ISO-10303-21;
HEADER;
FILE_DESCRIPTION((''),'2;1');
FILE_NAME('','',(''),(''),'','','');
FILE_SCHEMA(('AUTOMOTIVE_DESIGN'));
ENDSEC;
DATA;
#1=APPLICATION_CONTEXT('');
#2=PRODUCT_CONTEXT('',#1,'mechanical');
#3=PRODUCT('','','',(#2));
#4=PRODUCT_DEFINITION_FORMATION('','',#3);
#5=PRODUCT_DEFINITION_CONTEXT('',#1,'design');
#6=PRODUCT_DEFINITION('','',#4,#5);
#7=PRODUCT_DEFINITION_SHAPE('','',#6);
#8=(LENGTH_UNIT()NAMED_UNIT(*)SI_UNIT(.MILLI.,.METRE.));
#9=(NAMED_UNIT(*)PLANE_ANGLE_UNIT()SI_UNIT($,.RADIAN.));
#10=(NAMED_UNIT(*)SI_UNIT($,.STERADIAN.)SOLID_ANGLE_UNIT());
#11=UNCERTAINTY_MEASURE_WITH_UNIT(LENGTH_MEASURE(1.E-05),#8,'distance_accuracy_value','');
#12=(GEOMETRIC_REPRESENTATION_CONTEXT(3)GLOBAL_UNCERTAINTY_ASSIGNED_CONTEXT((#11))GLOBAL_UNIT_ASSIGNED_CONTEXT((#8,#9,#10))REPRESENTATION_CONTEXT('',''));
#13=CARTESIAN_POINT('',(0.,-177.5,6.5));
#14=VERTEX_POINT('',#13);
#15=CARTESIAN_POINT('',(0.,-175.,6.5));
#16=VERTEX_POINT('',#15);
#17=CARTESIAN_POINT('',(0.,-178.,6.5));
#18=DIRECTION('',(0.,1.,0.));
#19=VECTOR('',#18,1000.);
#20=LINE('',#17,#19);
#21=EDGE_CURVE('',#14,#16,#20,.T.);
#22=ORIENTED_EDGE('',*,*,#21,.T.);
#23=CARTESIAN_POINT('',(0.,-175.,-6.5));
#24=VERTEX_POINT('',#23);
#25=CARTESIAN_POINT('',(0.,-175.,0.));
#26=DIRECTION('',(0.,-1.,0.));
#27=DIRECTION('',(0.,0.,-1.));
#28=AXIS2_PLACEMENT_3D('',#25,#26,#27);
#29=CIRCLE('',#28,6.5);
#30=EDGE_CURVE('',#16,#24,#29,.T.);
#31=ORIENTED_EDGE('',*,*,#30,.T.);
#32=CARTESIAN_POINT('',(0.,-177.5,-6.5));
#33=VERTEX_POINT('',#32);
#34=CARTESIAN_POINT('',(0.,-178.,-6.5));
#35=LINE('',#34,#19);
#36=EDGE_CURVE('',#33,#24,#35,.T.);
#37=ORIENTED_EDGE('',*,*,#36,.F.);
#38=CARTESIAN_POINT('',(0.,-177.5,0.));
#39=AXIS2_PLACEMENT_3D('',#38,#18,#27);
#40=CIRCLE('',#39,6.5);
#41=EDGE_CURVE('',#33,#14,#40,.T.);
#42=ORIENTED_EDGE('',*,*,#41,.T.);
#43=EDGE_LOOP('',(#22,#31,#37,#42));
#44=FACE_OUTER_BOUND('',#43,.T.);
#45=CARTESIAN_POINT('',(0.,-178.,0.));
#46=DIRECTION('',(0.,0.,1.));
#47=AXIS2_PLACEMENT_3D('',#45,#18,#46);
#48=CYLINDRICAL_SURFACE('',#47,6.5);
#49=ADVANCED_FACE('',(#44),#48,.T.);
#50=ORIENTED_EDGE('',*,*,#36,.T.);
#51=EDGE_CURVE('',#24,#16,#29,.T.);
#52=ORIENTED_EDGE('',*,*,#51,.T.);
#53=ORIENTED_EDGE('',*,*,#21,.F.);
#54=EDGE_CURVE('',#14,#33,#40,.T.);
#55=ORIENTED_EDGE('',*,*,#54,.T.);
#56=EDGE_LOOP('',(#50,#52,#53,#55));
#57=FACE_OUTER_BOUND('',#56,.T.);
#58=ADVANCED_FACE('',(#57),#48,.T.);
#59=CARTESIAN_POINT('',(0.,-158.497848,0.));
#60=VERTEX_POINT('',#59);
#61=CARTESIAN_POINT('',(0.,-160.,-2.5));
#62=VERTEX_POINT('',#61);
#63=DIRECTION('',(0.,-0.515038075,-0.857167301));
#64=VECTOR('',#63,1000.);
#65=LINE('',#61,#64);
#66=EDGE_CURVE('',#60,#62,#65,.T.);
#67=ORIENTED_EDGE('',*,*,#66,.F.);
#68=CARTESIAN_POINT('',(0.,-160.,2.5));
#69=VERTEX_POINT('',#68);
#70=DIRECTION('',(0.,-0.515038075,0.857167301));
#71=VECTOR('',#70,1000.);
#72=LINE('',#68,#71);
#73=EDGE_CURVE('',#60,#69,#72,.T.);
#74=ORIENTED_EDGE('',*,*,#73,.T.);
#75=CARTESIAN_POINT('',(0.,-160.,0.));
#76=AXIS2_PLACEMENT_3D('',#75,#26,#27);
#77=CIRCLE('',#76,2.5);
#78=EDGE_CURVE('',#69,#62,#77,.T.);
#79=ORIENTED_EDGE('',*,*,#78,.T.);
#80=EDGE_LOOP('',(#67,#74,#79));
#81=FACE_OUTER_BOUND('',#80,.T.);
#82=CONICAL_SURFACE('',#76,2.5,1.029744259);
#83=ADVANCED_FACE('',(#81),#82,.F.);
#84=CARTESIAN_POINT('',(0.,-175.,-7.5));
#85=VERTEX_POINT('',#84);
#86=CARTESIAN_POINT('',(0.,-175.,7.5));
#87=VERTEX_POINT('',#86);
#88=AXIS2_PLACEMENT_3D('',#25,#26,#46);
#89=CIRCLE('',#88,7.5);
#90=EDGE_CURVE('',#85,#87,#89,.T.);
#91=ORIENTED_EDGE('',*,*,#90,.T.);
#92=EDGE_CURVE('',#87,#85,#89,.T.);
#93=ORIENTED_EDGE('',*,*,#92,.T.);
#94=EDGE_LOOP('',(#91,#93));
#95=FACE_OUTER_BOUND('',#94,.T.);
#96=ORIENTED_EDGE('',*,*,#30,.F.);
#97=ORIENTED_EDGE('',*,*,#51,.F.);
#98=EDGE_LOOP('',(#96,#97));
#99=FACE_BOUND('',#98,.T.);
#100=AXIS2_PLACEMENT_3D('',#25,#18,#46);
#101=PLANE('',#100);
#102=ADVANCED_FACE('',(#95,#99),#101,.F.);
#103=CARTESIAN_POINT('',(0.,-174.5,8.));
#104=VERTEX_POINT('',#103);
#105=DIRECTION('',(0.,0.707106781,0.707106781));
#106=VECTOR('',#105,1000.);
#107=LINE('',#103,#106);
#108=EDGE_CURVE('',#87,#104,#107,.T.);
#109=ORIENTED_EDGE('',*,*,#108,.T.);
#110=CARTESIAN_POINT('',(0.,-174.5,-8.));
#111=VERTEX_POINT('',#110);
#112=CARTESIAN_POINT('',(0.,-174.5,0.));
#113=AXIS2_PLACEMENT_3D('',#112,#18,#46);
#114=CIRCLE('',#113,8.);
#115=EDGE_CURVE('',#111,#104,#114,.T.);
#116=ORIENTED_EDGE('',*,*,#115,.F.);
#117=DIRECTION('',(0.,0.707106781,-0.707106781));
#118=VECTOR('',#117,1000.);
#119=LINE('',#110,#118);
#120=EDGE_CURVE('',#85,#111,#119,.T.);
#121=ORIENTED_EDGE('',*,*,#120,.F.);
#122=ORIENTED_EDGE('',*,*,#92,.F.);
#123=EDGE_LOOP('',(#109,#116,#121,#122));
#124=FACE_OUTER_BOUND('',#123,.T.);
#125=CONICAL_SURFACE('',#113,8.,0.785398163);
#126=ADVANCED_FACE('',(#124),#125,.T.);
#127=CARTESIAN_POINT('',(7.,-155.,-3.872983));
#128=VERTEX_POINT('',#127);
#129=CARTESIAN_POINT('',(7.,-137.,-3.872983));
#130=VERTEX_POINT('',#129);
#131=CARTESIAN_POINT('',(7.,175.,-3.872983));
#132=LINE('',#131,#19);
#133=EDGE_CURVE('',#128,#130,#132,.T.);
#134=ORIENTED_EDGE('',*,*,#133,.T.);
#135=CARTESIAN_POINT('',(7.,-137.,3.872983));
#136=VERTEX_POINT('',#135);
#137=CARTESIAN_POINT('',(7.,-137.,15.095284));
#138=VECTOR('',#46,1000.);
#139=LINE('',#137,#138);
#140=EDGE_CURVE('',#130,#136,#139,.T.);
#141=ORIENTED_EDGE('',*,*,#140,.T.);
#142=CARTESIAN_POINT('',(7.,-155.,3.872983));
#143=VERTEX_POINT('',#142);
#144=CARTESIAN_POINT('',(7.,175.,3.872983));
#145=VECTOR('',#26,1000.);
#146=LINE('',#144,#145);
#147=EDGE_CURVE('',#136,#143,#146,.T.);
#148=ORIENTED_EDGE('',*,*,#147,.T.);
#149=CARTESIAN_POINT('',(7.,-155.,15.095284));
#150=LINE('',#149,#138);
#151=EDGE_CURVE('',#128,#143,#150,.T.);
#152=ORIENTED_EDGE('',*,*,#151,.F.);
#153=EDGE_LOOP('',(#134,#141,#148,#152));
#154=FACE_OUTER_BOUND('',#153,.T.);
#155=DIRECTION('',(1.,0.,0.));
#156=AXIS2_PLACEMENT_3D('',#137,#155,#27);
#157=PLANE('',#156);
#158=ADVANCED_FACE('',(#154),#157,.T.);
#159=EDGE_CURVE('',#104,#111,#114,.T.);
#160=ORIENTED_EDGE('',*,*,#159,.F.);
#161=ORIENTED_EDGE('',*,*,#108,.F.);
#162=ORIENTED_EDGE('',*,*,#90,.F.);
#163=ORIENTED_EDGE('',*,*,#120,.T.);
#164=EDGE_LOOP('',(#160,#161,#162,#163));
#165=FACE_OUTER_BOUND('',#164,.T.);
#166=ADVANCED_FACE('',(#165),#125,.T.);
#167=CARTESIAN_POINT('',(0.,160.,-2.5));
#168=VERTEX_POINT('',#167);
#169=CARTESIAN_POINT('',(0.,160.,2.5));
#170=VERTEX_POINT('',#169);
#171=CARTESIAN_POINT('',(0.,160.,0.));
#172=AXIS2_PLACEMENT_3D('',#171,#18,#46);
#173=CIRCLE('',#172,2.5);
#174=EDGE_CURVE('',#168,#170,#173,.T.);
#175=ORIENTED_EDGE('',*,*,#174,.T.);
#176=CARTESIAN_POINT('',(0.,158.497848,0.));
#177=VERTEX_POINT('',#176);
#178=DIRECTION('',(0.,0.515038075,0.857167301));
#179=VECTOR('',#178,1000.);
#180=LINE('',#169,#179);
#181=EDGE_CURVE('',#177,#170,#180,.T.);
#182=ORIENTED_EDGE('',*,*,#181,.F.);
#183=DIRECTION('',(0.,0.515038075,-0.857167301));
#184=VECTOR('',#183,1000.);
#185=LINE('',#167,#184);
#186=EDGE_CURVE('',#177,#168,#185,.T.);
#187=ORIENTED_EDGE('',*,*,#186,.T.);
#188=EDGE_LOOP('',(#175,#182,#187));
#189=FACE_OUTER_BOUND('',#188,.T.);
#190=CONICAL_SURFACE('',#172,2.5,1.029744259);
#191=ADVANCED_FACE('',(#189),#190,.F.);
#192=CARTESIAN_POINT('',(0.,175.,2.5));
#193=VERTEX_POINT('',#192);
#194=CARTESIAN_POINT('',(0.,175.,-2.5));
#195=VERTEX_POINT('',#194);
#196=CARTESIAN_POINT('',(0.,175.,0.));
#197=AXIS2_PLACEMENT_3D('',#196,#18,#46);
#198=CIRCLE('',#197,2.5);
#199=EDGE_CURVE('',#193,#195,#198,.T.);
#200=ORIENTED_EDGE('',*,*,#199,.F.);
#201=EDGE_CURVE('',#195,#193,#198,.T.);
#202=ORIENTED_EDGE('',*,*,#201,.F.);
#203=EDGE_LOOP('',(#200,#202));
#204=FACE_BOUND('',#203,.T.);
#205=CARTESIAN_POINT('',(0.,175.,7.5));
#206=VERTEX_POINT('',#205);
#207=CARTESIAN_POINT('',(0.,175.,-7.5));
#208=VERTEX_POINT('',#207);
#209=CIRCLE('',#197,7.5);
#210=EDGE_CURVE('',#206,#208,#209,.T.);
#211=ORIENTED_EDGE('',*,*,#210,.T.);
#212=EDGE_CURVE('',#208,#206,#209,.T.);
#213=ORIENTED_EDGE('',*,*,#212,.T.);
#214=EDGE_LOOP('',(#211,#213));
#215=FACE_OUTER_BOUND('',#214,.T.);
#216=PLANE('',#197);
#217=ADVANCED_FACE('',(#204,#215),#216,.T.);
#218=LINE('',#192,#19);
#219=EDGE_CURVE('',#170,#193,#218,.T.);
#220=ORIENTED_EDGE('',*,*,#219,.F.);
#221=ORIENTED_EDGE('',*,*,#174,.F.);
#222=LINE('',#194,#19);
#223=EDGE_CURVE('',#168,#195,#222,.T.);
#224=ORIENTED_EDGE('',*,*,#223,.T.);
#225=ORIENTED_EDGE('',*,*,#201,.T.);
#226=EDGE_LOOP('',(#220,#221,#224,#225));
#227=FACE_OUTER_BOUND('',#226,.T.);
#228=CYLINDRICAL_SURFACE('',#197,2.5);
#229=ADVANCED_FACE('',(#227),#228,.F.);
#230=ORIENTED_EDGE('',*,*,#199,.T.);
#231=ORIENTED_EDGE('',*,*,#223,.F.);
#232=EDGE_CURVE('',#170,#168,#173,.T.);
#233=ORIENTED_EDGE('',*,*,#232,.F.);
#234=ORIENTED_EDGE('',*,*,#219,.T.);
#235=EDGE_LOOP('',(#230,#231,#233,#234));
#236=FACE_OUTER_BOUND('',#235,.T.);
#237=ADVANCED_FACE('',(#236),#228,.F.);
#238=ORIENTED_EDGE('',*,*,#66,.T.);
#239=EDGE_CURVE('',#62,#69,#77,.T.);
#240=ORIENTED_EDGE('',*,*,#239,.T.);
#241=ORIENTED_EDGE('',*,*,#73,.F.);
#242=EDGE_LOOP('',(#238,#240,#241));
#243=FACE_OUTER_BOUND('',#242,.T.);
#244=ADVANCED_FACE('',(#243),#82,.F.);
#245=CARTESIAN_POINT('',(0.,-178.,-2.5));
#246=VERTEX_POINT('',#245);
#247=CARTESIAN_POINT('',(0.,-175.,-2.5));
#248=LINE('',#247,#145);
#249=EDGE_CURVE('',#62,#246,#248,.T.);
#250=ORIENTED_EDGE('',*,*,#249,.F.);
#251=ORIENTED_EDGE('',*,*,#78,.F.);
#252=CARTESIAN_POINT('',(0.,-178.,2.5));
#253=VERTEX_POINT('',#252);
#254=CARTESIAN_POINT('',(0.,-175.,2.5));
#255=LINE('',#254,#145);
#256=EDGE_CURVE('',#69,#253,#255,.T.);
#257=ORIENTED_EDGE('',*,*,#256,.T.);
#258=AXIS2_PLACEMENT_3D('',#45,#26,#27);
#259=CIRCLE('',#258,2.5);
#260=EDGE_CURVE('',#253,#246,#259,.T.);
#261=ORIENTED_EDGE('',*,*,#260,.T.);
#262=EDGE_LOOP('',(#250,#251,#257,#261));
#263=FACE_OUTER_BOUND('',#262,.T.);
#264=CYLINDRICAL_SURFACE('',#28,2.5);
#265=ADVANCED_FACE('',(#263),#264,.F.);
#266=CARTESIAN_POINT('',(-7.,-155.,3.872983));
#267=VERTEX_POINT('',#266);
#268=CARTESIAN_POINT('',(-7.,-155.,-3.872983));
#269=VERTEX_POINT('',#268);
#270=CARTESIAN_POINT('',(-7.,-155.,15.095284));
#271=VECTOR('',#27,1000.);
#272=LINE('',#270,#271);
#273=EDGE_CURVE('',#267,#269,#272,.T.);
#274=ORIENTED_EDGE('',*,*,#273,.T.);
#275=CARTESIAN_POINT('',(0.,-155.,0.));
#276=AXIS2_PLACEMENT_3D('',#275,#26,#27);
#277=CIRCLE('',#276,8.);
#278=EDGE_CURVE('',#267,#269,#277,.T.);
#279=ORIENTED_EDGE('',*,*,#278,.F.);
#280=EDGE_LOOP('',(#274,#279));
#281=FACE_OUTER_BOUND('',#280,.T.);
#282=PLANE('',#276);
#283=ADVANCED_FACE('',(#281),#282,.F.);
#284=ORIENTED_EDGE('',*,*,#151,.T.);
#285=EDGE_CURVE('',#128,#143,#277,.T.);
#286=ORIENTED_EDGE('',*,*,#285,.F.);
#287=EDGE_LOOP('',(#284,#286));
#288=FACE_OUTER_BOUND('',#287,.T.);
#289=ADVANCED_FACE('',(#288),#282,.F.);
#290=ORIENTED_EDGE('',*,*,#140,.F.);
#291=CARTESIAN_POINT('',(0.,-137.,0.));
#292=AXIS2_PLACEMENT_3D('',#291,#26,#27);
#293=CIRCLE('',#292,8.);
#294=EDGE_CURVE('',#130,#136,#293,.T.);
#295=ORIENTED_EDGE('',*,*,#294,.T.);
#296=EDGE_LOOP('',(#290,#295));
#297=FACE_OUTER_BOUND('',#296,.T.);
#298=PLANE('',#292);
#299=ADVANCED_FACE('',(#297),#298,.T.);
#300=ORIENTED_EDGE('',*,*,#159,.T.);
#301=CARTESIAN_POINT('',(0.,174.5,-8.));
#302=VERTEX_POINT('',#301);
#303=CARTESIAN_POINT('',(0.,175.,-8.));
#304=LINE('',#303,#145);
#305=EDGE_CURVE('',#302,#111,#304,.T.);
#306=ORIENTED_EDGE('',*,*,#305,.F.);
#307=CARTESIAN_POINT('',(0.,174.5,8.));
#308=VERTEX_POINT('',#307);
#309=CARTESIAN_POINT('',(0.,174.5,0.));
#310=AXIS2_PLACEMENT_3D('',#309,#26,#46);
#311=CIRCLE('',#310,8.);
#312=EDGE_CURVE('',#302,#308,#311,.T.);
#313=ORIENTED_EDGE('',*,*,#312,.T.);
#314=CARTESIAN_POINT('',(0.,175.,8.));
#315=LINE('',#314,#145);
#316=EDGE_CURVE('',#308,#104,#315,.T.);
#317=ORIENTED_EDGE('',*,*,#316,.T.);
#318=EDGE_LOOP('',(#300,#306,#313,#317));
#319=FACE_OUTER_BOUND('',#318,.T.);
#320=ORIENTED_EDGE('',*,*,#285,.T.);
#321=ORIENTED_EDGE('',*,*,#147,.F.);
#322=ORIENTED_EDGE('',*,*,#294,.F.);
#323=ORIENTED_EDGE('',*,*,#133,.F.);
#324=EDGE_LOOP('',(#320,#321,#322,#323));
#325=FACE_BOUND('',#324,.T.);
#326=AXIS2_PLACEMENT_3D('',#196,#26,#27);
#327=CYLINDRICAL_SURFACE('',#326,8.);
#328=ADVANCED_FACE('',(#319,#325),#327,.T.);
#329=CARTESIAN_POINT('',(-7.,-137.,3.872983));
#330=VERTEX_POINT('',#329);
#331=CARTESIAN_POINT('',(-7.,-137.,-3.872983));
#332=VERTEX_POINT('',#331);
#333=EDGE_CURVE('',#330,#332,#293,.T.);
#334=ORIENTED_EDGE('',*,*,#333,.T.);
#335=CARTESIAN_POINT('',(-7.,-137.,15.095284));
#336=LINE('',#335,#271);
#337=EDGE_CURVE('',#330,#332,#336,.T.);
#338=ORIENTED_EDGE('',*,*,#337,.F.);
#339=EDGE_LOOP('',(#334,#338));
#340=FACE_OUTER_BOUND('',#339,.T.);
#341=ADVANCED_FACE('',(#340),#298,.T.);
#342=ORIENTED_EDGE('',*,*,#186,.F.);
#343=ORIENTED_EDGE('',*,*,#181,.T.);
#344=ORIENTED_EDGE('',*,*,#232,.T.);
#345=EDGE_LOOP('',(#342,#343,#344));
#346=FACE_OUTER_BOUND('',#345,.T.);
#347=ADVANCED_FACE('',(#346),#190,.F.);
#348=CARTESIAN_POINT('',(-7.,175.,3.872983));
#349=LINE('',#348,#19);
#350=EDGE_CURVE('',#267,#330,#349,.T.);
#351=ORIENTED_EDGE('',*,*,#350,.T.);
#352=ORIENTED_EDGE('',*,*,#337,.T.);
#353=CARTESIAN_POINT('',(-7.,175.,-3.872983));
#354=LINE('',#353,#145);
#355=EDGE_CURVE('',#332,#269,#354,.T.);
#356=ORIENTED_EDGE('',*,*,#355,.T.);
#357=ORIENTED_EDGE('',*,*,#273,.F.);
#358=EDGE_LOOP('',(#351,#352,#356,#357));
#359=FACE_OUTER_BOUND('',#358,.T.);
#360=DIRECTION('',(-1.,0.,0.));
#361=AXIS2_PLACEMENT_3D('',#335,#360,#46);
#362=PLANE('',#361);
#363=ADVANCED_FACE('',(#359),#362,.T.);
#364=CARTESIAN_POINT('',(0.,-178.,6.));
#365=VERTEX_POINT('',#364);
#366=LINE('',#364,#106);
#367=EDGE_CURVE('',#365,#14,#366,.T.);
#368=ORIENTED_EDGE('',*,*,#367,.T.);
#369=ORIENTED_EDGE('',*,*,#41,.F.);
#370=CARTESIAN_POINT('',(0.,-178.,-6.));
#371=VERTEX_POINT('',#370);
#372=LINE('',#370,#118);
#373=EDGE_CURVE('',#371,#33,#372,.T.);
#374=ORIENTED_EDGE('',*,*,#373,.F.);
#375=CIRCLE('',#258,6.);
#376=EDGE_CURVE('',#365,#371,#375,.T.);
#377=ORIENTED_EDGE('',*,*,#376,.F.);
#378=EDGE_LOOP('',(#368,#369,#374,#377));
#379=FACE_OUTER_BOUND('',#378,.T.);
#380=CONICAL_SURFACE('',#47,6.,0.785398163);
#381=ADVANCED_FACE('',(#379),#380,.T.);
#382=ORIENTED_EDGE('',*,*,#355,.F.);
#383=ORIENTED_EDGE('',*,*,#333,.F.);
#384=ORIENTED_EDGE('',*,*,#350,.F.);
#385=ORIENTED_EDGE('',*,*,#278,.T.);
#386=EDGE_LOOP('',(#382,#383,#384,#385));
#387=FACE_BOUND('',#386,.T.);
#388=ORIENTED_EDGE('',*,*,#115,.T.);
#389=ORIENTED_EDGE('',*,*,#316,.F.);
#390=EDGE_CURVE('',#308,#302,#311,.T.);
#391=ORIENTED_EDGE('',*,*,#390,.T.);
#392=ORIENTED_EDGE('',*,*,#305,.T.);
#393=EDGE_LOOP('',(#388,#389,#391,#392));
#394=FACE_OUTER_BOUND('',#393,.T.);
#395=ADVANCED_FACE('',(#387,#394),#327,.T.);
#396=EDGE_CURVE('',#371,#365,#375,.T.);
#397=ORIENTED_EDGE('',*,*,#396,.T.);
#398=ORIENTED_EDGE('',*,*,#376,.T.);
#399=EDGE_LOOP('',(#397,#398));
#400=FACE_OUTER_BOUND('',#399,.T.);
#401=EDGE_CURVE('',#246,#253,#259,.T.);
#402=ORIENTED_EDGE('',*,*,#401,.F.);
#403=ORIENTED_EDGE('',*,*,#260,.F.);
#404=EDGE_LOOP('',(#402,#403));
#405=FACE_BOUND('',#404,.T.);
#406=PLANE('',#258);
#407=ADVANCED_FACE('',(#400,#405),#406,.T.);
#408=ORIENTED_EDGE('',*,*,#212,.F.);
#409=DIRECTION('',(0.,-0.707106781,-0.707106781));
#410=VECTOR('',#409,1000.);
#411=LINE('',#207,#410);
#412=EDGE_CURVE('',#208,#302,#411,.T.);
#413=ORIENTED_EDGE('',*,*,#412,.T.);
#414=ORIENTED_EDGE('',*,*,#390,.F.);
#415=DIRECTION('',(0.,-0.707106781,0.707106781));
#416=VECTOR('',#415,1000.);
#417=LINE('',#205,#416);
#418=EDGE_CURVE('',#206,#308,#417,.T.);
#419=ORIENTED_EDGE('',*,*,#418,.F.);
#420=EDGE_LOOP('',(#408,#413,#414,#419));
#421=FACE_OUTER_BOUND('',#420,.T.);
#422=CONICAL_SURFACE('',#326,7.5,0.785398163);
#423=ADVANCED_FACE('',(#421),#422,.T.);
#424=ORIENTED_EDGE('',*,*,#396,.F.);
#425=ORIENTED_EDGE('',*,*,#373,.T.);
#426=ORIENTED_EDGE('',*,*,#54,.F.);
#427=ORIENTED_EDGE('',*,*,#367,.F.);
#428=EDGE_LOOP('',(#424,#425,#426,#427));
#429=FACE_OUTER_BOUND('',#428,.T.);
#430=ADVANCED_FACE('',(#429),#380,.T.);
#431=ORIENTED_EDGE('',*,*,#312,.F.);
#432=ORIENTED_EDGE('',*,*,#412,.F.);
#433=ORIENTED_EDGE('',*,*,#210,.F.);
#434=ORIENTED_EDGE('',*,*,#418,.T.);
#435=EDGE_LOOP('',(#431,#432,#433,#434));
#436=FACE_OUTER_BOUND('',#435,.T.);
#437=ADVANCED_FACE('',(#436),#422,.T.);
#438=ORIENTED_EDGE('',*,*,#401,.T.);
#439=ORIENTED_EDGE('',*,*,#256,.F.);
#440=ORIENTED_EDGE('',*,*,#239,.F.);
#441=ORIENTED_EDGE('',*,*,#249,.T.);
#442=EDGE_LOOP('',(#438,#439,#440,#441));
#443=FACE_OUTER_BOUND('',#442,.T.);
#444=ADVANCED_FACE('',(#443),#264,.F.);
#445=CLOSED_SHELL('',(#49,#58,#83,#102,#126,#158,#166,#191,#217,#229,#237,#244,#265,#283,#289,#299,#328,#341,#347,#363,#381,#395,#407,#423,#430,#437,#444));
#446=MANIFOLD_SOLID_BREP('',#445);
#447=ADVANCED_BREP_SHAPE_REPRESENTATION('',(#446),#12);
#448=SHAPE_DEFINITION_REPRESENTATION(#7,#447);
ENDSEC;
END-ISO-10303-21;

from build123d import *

# Parameters (mm, degrees)
SKETCH1_R             = 8
BOSS_EXTRUDE1_DEPTH   = 175
CUT_EXTRUDE1_START    = -20
SKETCH8_OUTSIDE_W     = 88.146
SKETCH8_OUTSIDE_H     = 88.146
SKETCH8_OUTSIDE_W_2   = 14
SKETCH8_OUTSIDE_H_2   = 30.19056833
CUT_EXTRUDE1_DEPTH    = 18
SKETCH9_R             = 6.5
BOSS_EXTRUDE2_DEPTH   = 3
M6_TAPPED_HOLE2_D     = 5
M6_TAPPED_HOLE2_DEPTH = 17
M6_TAPPED_HOLE2_TIP   = 1.502151548
CHAMFER1_SIZE         = 0.5
CHAMFER2_SIZE         = 0.5


with BuildPart() as part:
    # Sketch1 → Boss-Extrude1 (new, symmetric)
    with BuildSketch(Plane(origin=(0, 0, 0), x_dir=(1, 0, 0), z_dir=(0, 1, 0))):
        with Locations(Location((0, 0, 0), (0, 0, 270))):
            Circle(SKETCH1_R)
    extrude(amount=BOSS_EXTRUDE1_DEPTH, both=True)

    # Sketch7 → M6 Tapped Hole1 (revolve, cut)
    with BuildSketch(Plane(origin=(0, 175, 0), x_dir=(0, 0, 1), z_dir=(1, 0, 0))):
        Polygon((0, 0), (0, 16.502151548), (2.5, 15), (2.5, 0), align=None)
    m6_tapped_hole1 = revolve(axis=Axis((0, 181.35, 0), (0, -1, 0)), mode=Mode.SUBTRACT)

    # Mirror1: M6 Tapped Hole1 across plane
    add(m6_tapped_hole1.mirror(Plane.ZX), mode=Mode.SUBTRACT)

    # Sketch8 outside → Cut-Extrude1 (cut)
    with BuildSketch(Plane.XZ.offset(175).offset(CUT_EXTRUDE1_START)):
        Rectangle(SKETCH8_OUTSIDE_W, SKETCH8_OUTSIDE_H)
        Rectangle(SKETCH8_OUTSIDE_W_2, SKETCH8_OUTSIDE_H_2, mode=Mode.SUBTRACT)
    extrude(amount=-CUT_EXTRUDE1_DEPTH, mode=Mode.SUBTRACT)

    # Sketch9 → Boss-Extrude2 (add)
    with BuildSketch(Plane.XZ.offset(175)):
        with Locations(Location((0, 0, 0), (0, 0, 270))):
            Circle(SKETCH9_R)
    extrude(amount=BOSS_EXTRUDE2_DEPTH)

    # M6 Tapped Hole2
    with Locations(Plane(origin=(0, -178, 0), x_dir=(-1, 0, 0), z_dir=(0, -1, 0))):
        with Locations((0, 0)):
            Hole(M6_TAPPED_HOLE2_D / 2, depth=M6_TAPPED_HOLE2_DEPTH)
            with Locations((0, 0, -(M6_TAPPED_HOLE2_DEPTH + M6_TAPPED_HOLE2_TIP / 2))):  # 118° drill point
                Cone(0, M6_TAPPED_HOLE2_D / 2, M6_TAPPED_HOLE2_TIP, mode=Mode.SUBTRACT)

    # Chamfer1
    chamfer1_edges = [part.edges().sort_by_distance(p)[0] for p in [
        (0, -175, -8),
        (0, -178, 6.5),
    ]]
    chamfer(chamfer1_edges, length=CHAMFER1_SIZE)

    # Chamfer2
    chamfer2_edges = [part.edges().sort_by_distance(p)[0] for p in [
        (0, 175, -8),
    ]]
    chamfer(chamfer2_edges, length=CHAMFER2_SIZE)


solid = part.part
